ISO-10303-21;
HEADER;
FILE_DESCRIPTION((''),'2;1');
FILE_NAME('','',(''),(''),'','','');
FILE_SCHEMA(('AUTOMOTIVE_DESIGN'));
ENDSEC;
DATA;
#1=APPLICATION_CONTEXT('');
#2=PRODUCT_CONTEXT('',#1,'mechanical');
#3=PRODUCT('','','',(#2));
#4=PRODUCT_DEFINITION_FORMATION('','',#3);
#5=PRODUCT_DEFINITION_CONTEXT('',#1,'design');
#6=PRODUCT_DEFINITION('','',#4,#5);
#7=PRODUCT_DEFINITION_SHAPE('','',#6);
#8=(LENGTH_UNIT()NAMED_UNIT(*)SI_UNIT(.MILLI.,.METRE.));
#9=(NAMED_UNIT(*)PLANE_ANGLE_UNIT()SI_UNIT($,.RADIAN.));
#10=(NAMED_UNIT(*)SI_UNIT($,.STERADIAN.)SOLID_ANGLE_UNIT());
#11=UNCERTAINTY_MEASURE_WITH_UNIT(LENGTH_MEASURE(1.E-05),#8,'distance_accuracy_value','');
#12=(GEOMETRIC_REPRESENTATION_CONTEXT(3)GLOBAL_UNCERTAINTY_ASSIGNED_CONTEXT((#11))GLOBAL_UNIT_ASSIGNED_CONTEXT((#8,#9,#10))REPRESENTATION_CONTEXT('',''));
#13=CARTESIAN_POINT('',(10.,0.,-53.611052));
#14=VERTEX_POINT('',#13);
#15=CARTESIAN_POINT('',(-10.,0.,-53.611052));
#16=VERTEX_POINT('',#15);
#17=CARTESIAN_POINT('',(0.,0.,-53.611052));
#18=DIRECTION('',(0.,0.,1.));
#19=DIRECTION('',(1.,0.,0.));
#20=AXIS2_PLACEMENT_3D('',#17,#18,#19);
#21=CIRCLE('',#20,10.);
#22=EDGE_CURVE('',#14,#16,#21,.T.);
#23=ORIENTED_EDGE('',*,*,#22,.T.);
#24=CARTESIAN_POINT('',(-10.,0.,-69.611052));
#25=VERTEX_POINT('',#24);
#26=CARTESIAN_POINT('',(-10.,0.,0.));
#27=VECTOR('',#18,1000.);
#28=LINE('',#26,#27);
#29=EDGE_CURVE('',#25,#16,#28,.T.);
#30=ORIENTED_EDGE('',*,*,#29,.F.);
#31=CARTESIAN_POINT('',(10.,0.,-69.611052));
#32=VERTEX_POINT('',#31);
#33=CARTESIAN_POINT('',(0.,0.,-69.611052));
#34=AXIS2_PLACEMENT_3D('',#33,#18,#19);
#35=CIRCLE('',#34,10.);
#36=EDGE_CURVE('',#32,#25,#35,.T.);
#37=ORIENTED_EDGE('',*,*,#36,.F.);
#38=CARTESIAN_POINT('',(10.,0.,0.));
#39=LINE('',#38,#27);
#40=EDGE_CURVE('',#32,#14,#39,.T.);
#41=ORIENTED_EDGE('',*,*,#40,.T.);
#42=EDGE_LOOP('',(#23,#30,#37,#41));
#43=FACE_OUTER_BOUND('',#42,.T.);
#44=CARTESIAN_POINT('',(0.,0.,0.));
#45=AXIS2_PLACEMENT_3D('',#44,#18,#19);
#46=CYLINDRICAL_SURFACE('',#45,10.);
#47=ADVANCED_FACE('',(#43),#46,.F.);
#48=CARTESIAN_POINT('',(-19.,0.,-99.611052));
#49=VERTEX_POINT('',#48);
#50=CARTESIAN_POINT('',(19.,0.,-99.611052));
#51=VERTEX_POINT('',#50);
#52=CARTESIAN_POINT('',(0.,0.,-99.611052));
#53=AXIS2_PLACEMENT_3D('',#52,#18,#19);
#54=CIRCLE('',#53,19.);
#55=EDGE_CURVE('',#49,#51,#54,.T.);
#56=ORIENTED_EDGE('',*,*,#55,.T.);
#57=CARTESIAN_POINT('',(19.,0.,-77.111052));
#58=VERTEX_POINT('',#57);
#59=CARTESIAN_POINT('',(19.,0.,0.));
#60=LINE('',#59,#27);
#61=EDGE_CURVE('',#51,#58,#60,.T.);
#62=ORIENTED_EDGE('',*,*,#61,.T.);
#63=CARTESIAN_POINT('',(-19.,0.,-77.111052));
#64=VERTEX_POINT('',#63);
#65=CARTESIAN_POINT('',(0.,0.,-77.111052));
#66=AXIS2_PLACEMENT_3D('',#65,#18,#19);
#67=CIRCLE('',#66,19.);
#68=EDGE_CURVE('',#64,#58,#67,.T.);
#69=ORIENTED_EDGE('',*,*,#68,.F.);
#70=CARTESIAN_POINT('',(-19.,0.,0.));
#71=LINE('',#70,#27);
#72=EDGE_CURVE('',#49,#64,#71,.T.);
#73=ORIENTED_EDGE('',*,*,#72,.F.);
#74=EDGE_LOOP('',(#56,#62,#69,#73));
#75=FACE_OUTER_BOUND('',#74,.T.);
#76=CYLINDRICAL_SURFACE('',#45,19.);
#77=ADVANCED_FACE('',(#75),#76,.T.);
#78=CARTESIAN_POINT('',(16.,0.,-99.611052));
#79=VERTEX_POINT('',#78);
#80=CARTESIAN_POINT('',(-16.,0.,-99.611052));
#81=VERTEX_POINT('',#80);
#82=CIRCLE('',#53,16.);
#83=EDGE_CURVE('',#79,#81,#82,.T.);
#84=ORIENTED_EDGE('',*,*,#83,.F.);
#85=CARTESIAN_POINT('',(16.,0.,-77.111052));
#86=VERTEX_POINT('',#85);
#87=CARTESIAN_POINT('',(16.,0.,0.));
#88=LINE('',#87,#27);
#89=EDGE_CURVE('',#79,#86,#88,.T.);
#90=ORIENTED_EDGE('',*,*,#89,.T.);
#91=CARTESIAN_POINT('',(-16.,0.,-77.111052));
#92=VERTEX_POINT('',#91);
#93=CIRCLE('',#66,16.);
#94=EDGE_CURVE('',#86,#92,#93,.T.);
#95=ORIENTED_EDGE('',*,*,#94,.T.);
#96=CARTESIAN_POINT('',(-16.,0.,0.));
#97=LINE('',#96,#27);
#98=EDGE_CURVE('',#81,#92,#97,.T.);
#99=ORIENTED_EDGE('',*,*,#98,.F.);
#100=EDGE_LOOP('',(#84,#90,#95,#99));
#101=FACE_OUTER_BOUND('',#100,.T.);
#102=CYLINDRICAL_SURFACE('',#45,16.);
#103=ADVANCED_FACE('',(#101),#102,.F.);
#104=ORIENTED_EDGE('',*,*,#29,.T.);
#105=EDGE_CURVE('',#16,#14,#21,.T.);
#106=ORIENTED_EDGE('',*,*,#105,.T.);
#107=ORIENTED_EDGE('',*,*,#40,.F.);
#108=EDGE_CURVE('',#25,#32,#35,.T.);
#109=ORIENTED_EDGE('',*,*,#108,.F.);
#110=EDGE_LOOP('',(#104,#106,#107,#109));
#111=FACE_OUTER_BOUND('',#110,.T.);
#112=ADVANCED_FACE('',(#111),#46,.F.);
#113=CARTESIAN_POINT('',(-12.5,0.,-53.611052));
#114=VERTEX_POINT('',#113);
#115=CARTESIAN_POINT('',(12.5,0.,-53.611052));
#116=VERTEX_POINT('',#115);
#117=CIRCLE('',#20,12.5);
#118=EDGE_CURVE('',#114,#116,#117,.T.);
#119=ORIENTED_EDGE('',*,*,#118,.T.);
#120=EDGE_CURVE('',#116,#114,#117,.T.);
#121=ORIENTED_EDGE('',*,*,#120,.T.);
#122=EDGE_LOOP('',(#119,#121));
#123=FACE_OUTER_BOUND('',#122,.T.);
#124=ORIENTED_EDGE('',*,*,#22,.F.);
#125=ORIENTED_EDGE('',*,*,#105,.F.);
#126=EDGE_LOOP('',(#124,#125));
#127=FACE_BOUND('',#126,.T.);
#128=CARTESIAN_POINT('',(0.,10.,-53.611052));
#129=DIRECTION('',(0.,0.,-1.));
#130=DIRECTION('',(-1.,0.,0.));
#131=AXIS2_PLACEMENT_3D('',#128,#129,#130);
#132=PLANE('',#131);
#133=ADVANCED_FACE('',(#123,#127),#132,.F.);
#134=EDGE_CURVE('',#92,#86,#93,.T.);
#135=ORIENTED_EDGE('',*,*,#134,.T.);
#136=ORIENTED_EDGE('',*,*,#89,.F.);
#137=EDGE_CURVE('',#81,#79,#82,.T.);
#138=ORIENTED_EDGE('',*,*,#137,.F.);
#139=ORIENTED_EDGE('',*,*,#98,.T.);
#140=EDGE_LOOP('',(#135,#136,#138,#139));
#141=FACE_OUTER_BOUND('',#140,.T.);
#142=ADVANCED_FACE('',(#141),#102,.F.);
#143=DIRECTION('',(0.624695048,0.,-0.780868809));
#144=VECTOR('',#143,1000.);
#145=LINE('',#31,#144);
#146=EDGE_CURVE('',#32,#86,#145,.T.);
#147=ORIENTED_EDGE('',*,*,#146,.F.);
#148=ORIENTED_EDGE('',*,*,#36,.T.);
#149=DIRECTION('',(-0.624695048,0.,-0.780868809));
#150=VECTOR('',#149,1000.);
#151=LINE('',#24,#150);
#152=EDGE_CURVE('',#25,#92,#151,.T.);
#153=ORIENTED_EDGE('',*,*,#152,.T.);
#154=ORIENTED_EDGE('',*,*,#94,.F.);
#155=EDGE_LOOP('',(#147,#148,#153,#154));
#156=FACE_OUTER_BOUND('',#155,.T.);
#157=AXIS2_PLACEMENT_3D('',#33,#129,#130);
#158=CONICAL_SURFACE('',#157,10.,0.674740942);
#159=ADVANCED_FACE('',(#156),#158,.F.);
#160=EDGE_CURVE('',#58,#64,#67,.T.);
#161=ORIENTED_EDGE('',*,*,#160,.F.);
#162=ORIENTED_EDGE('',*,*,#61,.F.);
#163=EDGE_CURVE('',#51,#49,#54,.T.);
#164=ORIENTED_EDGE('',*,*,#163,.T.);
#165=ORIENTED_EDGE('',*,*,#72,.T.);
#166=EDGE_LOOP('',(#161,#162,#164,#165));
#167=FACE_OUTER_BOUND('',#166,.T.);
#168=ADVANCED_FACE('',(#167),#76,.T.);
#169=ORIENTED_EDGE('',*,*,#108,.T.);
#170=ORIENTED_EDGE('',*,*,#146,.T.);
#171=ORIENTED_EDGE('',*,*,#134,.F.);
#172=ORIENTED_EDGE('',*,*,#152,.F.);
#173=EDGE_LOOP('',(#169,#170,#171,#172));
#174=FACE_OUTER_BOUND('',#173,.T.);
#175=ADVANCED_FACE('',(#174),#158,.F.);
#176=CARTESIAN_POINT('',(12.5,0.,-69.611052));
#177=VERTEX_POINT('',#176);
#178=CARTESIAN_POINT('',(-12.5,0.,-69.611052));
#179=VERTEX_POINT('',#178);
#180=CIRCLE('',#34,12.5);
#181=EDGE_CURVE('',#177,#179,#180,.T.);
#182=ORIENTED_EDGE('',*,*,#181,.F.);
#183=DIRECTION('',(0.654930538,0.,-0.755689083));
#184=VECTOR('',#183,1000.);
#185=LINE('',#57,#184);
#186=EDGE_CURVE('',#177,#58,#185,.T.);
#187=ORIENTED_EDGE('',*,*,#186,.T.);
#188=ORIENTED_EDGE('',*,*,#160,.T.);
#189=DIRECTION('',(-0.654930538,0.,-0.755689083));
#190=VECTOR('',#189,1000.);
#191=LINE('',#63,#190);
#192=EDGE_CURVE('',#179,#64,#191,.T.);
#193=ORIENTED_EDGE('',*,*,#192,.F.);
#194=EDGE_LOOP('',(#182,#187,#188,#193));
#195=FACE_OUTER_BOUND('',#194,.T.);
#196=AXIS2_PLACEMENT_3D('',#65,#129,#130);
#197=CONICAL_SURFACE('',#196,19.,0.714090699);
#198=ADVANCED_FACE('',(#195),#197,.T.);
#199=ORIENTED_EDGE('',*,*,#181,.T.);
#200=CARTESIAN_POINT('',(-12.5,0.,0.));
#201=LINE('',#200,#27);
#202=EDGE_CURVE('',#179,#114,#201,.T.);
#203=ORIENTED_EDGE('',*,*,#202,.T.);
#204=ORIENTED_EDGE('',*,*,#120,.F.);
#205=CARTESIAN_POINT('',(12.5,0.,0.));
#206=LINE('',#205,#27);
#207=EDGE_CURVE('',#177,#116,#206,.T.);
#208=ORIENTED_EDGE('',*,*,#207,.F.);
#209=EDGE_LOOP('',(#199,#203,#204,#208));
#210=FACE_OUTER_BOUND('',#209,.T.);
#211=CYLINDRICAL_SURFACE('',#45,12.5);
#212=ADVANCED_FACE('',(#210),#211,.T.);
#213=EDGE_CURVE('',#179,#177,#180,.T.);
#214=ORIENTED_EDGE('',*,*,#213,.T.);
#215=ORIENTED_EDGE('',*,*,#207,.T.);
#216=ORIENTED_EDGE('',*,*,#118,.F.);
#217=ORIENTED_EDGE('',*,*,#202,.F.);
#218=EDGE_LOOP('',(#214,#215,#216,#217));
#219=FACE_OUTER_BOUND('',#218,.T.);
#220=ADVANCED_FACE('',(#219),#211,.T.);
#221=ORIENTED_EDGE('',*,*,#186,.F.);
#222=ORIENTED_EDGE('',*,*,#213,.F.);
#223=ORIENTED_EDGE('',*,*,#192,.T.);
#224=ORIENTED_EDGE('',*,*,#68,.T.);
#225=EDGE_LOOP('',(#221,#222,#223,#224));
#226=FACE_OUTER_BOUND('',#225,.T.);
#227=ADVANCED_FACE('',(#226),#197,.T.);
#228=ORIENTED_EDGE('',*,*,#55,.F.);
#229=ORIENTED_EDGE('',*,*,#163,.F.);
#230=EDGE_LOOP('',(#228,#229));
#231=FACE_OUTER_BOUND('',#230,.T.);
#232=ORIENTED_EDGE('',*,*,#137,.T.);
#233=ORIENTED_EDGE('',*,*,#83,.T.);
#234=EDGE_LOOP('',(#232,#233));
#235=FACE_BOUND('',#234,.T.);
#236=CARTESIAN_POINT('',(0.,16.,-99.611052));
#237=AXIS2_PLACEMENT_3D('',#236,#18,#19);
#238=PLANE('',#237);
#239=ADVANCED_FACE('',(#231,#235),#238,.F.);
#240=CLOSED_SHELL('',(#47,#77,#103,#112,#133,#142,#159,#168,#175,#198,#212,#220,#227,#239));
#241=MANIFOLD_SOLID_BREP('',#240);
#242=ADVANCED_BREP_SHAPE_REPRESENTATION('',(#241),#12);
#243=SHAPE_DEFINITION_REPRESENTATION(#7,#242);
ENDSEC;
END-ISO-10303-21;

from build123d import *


with BuildPart() as part:
    # 草图1 → 旋转1 (revolve)
    with BuildSketch(Plane(origin=(0, 0, 0), x_dir=(0, 0, -1), z_dir=(1, 0, 0)), mode=Mode.PRIVATE) as revolve_1_sk:
        Polygon((53.611052376, 10), (69.611052376, 10), (77.111052376, 16), (99.611052376, 16), (99.611052376, 19), (77.111052376, 19), (69.611052376, 12.5), (53.611052376, 12.5), align=None)
    revolve(revolve_1_sk.sketch.rotate(Axis((0, 0, 0), (0, 0, -1)), 90), axis=Axis((0, 0, 0), (0, 0, -1)))


solid = part.part
